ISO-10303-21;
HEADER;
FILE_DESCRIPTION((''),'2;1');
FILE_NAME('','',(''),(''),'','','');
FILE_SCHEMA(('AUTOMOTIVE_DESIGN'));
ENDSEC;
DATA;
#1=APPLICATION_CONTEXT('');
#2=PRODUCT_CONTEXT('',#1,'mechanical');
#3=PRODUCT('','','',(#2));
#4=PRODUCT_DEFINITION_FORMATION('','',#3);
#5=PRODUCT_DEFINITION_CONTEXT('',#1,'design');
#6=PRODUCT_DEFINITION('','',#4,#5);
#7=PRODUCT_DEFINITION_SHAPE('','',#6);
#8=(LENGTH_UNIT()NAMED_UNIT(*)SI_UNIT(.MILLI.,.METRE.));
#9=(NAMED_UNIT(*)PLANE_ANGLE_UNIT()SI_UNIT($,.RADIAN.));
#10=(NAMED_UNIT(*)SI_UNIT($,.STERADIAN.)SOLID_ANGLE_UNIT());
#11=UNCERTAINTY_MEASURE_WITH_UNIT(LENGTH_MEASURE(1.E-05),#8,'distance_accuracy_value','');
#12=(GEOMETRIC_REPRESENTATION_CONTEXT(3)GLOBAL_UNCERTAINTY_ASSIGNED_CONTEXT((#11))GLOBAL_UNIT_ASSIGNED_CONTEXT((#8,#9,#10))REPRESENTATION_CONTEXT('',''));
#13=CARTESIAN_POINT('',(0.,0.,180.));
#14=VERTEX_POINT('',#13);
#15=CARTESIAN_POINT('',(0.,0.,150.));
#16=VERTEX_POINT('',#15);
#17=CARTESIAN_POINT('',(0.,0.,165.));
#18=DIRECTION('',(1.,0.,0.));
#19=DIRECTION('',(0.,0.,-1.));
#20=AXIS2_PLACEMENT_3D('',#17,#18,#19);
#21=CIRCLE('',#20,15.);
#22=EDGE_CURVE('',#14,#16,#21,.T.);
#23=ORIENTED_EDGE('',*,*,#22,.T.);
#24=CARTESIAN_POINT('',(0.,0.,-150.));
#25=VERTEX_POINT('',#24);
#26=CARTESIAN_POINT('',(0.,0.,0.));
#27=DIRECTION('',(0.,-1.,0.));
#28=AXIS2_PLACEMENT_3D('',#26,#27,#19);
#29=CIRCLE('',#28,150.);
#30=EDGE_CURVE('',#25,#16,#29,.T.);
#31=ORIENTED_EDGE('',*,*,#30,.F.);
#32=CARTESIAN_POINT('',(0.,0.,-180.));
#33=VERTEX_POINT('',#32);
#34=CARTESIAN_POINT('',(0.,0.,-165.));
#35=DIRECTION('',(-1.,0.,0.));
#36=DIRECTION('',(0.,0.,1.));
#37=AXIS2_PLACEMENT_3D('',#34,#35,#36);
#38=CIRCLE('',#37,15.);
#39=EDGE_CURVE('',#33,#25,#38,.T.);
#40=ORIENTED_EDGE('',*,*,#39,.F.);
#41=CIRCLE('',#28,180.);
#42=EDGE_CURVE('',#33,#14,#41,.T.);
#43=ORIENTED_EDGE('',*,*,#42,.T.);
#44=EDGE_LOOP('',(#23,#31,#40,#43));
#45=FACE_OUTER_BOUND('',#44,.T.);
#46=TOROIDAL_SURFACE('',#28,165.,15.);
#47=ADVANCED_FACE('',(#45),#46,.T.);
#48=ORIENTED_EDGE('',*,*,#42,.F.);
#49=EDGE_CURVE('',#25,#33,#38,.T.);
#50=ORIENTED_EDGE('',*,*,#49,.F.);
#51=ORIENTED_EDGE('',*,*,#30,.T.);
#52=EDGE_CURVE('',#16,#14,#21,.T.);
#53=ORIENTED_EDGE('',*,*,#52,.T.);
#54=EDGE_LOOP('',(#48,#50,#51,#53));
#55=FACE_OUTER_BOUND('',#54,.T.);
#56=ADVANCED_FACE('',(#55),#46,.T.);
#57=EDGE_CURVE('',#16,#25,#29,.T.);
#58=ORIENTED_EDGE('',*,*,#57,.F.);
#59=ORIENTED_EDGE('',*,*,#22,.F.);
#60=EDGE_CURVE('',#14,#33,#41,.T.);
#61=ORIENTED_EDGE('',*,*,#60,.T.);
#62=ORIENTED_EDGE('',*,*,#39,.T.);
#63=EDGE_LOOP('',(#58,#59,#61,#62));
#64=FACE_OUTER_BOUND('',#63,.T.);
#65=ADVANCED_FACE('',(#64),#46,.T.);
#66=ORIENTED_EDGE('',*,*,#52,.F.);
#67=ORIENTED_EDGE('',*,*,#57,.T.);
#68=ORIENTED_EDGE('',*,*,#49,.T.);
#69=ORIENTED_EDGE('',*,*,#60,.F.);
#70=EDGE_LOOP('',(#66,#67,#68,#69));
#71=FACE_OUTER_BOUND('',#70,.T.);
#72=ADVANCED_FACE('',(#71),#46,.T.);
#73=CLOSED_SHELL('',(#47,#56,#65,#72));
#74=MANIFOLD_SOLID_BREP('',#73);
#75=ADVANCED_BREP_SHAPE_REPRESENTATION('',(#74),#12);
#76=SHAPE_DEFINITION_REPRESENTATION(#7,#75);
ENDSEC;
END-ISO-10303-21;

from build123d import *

# Parameters (mm, degrees)
SKETCH1_R = 15


with BuildPart() as part:
    # Sketch1 → Revolve1 (revolve)
    with BuildSketch(Plane.XY, mode=Mode.PRIVATE) as revolve1_sk:
        with Locations((165, 0)):
            Circle(SKETCH1_R)
    revolve(revolve1_sk.sketch.rotate(Axis((0, 0, 0), (0, 1, 0)), 90), axis=Axis((0, 0, 0), (0, 1, 0)))


solid = part.part
